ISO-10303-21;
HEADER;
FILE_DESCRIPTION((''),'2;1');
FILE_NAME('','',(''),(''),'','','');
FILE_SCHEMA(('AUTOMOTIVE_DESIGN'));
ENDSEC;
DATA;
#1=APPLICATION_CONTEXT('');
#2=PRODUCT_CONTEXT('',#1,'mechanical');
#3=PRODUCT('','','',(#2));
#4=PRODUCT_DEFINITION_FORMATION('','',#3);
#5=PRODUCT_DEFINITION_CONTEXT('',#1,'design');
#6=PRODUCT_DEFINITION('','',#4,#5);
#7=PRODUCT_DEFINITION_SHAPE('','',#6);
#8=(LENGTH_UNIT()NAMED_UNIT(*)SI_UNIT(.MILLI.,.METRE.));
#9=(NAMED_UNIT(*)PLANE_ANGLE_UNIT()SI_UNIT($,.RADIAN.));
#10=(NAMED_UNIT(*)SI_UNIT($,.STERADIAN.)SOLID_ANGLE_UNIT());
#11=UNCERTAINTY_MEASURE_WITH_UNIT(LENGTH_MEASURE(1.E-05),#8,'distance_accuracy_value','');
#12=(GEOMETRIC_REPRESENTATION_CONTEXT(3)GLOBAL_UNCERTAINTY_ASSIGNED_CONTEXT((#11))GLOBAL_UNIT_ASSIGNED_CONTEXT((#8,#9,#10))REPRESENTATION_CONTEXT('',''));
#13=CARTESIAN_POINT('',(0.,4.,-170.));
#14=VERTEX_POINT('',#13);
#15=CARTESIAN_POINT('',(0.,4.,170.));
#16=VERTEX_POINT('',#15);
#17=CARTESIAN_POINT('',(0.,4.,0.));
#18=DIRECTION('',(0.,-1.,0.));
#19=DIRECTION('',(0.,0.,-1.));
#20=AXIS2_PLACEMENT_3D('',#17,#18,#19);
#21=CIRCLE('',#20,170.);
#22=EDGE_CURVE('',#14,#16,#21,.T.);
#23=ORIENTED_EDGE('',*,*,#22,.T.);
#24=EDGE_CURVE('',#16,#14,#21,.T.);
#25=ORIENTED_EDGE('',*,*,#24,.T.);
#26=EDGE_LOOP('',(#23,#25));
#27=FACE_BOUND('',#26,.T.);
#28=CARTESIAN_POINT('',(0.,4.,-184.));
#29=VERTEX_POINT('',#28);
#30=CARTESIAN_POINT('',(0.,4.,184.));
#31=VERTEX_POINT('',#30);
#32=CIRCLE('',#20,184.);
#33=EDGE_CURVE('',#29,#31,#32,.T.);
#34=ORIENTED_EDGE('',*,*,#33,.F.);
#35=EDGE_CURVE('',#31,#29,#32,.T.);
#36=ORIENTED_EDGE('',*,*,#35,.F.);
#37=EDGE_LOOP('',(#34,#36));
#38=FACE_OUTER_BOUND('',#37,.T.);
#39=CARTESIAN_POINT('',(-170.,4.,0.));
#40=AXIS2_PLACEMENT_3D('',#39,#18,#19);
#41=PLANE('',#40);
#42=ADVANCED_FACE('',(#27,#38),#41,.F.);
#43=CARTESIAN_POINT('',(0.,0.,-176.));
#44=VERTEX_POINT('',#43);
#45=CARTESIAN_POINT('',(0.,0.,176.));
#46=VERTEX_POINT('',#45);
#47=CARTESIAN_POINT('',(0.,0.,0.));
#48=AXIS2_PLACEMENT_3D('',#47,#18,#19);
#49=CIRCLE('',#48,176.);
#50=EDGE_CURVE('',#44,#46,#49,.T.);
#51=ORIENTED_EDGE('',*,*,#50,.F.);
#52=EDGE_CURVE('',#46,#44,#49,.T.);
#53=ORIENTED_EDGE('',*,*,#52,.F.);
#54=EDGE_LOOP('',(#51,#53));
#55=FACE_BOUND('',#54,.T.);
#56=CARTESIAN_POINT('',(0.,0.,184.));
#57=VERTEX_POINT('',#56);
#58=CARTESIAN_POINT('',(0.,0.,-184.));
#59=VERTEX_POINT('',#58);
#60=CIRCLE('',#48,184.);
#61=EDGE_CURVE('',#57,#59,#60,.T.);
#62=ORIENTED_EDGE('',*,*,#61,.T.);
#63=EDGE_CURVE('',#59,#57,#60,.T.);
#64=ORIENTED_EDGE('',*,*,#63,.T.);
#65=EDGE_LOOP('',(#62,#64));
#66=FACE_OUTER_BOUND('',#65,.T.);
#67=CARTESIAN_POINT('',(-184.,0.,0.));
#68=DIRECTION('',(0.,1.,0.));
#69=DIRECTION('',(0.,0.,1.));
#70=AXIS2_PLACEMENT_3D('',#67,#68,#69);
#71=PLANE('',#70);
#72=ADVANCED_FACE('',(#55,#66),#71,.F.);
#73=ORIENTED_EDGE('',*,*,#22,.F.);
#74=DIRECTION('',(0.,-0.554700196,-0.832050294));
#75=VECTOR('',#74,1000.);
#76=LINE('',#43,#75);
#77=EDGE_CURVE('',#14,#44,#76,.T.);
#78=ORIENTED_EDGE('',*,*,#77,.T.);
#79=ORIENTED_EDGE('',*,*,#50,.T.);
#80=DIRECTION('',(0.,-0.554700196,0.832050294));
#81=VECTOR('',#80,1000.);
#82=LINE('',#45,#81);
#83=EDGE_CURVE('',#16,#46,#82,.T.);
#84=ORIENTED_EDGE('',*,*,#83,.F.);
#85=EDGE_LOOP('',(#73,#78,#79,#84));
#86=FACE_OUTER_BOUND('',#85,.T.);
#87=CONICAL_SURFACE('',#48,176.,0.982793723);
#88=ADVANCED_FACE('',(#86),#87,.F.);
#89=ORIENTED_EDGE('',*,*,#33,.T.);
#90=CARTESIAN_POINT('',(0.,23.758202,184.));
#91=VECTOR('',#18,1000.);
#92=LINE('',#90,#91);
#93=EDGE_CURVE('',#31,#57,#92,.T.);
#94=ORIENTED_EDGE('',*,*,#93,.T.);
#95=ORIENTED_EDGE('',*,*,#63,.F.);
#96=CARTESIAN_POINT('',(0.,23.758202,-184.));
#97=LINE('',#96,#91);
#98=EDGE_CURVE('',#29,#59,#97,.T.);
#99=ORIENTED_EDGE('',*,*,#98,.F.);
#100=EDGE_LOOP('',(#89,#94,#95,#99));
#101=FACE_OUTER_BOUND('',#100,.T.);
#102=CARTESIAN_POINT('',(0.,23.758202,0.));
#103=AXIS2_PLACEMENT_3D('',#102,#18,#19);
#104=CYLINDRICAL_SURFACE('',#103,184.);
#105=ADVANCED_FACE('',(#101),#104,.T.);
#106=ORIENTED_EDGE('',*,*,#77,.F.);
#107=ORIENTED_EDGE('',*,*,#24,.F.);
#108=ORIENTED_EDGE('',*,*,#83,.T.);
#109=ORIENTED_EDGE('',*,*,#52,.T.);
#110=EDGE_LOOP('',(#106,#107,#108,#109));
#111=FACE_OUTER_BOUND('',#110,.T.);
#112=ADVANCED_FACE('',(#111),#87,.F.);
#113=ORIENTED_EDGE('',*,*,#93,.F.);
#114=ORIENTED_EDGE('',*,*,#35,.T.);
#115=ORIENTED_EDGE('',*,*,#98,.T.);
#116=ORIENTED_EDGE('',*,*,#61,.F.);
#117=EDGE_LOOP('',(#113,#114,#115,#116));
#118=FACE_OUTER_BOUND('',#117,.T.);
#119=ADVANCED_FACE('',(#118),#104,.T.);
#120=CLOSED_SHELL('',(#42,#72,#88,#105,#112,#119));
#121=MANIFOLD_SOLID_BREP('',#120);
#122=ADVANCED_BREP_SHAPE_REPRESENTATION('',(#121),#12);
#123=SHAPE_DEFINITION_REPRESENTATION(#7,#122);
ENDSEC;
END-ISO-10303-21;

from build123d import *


with BuildPart() as part:
    # Sketch1 → Revolve1 (revolve)
    with BuildSketch(Plane.XY, mode=Mode.PRIVATE) as revolve1_sk:
        Polygon((-170, 4), (-184, 4), (-184, 0), (-176, 0), align=None)
    revolve(revolve1_sk.sketch.rotate(Axis((0, 23.75820198, 0), (0, 1, 0)), 270), axis=Axis((0, 23.75820198, 0), (0, 1, 0)))


solid = part.part
